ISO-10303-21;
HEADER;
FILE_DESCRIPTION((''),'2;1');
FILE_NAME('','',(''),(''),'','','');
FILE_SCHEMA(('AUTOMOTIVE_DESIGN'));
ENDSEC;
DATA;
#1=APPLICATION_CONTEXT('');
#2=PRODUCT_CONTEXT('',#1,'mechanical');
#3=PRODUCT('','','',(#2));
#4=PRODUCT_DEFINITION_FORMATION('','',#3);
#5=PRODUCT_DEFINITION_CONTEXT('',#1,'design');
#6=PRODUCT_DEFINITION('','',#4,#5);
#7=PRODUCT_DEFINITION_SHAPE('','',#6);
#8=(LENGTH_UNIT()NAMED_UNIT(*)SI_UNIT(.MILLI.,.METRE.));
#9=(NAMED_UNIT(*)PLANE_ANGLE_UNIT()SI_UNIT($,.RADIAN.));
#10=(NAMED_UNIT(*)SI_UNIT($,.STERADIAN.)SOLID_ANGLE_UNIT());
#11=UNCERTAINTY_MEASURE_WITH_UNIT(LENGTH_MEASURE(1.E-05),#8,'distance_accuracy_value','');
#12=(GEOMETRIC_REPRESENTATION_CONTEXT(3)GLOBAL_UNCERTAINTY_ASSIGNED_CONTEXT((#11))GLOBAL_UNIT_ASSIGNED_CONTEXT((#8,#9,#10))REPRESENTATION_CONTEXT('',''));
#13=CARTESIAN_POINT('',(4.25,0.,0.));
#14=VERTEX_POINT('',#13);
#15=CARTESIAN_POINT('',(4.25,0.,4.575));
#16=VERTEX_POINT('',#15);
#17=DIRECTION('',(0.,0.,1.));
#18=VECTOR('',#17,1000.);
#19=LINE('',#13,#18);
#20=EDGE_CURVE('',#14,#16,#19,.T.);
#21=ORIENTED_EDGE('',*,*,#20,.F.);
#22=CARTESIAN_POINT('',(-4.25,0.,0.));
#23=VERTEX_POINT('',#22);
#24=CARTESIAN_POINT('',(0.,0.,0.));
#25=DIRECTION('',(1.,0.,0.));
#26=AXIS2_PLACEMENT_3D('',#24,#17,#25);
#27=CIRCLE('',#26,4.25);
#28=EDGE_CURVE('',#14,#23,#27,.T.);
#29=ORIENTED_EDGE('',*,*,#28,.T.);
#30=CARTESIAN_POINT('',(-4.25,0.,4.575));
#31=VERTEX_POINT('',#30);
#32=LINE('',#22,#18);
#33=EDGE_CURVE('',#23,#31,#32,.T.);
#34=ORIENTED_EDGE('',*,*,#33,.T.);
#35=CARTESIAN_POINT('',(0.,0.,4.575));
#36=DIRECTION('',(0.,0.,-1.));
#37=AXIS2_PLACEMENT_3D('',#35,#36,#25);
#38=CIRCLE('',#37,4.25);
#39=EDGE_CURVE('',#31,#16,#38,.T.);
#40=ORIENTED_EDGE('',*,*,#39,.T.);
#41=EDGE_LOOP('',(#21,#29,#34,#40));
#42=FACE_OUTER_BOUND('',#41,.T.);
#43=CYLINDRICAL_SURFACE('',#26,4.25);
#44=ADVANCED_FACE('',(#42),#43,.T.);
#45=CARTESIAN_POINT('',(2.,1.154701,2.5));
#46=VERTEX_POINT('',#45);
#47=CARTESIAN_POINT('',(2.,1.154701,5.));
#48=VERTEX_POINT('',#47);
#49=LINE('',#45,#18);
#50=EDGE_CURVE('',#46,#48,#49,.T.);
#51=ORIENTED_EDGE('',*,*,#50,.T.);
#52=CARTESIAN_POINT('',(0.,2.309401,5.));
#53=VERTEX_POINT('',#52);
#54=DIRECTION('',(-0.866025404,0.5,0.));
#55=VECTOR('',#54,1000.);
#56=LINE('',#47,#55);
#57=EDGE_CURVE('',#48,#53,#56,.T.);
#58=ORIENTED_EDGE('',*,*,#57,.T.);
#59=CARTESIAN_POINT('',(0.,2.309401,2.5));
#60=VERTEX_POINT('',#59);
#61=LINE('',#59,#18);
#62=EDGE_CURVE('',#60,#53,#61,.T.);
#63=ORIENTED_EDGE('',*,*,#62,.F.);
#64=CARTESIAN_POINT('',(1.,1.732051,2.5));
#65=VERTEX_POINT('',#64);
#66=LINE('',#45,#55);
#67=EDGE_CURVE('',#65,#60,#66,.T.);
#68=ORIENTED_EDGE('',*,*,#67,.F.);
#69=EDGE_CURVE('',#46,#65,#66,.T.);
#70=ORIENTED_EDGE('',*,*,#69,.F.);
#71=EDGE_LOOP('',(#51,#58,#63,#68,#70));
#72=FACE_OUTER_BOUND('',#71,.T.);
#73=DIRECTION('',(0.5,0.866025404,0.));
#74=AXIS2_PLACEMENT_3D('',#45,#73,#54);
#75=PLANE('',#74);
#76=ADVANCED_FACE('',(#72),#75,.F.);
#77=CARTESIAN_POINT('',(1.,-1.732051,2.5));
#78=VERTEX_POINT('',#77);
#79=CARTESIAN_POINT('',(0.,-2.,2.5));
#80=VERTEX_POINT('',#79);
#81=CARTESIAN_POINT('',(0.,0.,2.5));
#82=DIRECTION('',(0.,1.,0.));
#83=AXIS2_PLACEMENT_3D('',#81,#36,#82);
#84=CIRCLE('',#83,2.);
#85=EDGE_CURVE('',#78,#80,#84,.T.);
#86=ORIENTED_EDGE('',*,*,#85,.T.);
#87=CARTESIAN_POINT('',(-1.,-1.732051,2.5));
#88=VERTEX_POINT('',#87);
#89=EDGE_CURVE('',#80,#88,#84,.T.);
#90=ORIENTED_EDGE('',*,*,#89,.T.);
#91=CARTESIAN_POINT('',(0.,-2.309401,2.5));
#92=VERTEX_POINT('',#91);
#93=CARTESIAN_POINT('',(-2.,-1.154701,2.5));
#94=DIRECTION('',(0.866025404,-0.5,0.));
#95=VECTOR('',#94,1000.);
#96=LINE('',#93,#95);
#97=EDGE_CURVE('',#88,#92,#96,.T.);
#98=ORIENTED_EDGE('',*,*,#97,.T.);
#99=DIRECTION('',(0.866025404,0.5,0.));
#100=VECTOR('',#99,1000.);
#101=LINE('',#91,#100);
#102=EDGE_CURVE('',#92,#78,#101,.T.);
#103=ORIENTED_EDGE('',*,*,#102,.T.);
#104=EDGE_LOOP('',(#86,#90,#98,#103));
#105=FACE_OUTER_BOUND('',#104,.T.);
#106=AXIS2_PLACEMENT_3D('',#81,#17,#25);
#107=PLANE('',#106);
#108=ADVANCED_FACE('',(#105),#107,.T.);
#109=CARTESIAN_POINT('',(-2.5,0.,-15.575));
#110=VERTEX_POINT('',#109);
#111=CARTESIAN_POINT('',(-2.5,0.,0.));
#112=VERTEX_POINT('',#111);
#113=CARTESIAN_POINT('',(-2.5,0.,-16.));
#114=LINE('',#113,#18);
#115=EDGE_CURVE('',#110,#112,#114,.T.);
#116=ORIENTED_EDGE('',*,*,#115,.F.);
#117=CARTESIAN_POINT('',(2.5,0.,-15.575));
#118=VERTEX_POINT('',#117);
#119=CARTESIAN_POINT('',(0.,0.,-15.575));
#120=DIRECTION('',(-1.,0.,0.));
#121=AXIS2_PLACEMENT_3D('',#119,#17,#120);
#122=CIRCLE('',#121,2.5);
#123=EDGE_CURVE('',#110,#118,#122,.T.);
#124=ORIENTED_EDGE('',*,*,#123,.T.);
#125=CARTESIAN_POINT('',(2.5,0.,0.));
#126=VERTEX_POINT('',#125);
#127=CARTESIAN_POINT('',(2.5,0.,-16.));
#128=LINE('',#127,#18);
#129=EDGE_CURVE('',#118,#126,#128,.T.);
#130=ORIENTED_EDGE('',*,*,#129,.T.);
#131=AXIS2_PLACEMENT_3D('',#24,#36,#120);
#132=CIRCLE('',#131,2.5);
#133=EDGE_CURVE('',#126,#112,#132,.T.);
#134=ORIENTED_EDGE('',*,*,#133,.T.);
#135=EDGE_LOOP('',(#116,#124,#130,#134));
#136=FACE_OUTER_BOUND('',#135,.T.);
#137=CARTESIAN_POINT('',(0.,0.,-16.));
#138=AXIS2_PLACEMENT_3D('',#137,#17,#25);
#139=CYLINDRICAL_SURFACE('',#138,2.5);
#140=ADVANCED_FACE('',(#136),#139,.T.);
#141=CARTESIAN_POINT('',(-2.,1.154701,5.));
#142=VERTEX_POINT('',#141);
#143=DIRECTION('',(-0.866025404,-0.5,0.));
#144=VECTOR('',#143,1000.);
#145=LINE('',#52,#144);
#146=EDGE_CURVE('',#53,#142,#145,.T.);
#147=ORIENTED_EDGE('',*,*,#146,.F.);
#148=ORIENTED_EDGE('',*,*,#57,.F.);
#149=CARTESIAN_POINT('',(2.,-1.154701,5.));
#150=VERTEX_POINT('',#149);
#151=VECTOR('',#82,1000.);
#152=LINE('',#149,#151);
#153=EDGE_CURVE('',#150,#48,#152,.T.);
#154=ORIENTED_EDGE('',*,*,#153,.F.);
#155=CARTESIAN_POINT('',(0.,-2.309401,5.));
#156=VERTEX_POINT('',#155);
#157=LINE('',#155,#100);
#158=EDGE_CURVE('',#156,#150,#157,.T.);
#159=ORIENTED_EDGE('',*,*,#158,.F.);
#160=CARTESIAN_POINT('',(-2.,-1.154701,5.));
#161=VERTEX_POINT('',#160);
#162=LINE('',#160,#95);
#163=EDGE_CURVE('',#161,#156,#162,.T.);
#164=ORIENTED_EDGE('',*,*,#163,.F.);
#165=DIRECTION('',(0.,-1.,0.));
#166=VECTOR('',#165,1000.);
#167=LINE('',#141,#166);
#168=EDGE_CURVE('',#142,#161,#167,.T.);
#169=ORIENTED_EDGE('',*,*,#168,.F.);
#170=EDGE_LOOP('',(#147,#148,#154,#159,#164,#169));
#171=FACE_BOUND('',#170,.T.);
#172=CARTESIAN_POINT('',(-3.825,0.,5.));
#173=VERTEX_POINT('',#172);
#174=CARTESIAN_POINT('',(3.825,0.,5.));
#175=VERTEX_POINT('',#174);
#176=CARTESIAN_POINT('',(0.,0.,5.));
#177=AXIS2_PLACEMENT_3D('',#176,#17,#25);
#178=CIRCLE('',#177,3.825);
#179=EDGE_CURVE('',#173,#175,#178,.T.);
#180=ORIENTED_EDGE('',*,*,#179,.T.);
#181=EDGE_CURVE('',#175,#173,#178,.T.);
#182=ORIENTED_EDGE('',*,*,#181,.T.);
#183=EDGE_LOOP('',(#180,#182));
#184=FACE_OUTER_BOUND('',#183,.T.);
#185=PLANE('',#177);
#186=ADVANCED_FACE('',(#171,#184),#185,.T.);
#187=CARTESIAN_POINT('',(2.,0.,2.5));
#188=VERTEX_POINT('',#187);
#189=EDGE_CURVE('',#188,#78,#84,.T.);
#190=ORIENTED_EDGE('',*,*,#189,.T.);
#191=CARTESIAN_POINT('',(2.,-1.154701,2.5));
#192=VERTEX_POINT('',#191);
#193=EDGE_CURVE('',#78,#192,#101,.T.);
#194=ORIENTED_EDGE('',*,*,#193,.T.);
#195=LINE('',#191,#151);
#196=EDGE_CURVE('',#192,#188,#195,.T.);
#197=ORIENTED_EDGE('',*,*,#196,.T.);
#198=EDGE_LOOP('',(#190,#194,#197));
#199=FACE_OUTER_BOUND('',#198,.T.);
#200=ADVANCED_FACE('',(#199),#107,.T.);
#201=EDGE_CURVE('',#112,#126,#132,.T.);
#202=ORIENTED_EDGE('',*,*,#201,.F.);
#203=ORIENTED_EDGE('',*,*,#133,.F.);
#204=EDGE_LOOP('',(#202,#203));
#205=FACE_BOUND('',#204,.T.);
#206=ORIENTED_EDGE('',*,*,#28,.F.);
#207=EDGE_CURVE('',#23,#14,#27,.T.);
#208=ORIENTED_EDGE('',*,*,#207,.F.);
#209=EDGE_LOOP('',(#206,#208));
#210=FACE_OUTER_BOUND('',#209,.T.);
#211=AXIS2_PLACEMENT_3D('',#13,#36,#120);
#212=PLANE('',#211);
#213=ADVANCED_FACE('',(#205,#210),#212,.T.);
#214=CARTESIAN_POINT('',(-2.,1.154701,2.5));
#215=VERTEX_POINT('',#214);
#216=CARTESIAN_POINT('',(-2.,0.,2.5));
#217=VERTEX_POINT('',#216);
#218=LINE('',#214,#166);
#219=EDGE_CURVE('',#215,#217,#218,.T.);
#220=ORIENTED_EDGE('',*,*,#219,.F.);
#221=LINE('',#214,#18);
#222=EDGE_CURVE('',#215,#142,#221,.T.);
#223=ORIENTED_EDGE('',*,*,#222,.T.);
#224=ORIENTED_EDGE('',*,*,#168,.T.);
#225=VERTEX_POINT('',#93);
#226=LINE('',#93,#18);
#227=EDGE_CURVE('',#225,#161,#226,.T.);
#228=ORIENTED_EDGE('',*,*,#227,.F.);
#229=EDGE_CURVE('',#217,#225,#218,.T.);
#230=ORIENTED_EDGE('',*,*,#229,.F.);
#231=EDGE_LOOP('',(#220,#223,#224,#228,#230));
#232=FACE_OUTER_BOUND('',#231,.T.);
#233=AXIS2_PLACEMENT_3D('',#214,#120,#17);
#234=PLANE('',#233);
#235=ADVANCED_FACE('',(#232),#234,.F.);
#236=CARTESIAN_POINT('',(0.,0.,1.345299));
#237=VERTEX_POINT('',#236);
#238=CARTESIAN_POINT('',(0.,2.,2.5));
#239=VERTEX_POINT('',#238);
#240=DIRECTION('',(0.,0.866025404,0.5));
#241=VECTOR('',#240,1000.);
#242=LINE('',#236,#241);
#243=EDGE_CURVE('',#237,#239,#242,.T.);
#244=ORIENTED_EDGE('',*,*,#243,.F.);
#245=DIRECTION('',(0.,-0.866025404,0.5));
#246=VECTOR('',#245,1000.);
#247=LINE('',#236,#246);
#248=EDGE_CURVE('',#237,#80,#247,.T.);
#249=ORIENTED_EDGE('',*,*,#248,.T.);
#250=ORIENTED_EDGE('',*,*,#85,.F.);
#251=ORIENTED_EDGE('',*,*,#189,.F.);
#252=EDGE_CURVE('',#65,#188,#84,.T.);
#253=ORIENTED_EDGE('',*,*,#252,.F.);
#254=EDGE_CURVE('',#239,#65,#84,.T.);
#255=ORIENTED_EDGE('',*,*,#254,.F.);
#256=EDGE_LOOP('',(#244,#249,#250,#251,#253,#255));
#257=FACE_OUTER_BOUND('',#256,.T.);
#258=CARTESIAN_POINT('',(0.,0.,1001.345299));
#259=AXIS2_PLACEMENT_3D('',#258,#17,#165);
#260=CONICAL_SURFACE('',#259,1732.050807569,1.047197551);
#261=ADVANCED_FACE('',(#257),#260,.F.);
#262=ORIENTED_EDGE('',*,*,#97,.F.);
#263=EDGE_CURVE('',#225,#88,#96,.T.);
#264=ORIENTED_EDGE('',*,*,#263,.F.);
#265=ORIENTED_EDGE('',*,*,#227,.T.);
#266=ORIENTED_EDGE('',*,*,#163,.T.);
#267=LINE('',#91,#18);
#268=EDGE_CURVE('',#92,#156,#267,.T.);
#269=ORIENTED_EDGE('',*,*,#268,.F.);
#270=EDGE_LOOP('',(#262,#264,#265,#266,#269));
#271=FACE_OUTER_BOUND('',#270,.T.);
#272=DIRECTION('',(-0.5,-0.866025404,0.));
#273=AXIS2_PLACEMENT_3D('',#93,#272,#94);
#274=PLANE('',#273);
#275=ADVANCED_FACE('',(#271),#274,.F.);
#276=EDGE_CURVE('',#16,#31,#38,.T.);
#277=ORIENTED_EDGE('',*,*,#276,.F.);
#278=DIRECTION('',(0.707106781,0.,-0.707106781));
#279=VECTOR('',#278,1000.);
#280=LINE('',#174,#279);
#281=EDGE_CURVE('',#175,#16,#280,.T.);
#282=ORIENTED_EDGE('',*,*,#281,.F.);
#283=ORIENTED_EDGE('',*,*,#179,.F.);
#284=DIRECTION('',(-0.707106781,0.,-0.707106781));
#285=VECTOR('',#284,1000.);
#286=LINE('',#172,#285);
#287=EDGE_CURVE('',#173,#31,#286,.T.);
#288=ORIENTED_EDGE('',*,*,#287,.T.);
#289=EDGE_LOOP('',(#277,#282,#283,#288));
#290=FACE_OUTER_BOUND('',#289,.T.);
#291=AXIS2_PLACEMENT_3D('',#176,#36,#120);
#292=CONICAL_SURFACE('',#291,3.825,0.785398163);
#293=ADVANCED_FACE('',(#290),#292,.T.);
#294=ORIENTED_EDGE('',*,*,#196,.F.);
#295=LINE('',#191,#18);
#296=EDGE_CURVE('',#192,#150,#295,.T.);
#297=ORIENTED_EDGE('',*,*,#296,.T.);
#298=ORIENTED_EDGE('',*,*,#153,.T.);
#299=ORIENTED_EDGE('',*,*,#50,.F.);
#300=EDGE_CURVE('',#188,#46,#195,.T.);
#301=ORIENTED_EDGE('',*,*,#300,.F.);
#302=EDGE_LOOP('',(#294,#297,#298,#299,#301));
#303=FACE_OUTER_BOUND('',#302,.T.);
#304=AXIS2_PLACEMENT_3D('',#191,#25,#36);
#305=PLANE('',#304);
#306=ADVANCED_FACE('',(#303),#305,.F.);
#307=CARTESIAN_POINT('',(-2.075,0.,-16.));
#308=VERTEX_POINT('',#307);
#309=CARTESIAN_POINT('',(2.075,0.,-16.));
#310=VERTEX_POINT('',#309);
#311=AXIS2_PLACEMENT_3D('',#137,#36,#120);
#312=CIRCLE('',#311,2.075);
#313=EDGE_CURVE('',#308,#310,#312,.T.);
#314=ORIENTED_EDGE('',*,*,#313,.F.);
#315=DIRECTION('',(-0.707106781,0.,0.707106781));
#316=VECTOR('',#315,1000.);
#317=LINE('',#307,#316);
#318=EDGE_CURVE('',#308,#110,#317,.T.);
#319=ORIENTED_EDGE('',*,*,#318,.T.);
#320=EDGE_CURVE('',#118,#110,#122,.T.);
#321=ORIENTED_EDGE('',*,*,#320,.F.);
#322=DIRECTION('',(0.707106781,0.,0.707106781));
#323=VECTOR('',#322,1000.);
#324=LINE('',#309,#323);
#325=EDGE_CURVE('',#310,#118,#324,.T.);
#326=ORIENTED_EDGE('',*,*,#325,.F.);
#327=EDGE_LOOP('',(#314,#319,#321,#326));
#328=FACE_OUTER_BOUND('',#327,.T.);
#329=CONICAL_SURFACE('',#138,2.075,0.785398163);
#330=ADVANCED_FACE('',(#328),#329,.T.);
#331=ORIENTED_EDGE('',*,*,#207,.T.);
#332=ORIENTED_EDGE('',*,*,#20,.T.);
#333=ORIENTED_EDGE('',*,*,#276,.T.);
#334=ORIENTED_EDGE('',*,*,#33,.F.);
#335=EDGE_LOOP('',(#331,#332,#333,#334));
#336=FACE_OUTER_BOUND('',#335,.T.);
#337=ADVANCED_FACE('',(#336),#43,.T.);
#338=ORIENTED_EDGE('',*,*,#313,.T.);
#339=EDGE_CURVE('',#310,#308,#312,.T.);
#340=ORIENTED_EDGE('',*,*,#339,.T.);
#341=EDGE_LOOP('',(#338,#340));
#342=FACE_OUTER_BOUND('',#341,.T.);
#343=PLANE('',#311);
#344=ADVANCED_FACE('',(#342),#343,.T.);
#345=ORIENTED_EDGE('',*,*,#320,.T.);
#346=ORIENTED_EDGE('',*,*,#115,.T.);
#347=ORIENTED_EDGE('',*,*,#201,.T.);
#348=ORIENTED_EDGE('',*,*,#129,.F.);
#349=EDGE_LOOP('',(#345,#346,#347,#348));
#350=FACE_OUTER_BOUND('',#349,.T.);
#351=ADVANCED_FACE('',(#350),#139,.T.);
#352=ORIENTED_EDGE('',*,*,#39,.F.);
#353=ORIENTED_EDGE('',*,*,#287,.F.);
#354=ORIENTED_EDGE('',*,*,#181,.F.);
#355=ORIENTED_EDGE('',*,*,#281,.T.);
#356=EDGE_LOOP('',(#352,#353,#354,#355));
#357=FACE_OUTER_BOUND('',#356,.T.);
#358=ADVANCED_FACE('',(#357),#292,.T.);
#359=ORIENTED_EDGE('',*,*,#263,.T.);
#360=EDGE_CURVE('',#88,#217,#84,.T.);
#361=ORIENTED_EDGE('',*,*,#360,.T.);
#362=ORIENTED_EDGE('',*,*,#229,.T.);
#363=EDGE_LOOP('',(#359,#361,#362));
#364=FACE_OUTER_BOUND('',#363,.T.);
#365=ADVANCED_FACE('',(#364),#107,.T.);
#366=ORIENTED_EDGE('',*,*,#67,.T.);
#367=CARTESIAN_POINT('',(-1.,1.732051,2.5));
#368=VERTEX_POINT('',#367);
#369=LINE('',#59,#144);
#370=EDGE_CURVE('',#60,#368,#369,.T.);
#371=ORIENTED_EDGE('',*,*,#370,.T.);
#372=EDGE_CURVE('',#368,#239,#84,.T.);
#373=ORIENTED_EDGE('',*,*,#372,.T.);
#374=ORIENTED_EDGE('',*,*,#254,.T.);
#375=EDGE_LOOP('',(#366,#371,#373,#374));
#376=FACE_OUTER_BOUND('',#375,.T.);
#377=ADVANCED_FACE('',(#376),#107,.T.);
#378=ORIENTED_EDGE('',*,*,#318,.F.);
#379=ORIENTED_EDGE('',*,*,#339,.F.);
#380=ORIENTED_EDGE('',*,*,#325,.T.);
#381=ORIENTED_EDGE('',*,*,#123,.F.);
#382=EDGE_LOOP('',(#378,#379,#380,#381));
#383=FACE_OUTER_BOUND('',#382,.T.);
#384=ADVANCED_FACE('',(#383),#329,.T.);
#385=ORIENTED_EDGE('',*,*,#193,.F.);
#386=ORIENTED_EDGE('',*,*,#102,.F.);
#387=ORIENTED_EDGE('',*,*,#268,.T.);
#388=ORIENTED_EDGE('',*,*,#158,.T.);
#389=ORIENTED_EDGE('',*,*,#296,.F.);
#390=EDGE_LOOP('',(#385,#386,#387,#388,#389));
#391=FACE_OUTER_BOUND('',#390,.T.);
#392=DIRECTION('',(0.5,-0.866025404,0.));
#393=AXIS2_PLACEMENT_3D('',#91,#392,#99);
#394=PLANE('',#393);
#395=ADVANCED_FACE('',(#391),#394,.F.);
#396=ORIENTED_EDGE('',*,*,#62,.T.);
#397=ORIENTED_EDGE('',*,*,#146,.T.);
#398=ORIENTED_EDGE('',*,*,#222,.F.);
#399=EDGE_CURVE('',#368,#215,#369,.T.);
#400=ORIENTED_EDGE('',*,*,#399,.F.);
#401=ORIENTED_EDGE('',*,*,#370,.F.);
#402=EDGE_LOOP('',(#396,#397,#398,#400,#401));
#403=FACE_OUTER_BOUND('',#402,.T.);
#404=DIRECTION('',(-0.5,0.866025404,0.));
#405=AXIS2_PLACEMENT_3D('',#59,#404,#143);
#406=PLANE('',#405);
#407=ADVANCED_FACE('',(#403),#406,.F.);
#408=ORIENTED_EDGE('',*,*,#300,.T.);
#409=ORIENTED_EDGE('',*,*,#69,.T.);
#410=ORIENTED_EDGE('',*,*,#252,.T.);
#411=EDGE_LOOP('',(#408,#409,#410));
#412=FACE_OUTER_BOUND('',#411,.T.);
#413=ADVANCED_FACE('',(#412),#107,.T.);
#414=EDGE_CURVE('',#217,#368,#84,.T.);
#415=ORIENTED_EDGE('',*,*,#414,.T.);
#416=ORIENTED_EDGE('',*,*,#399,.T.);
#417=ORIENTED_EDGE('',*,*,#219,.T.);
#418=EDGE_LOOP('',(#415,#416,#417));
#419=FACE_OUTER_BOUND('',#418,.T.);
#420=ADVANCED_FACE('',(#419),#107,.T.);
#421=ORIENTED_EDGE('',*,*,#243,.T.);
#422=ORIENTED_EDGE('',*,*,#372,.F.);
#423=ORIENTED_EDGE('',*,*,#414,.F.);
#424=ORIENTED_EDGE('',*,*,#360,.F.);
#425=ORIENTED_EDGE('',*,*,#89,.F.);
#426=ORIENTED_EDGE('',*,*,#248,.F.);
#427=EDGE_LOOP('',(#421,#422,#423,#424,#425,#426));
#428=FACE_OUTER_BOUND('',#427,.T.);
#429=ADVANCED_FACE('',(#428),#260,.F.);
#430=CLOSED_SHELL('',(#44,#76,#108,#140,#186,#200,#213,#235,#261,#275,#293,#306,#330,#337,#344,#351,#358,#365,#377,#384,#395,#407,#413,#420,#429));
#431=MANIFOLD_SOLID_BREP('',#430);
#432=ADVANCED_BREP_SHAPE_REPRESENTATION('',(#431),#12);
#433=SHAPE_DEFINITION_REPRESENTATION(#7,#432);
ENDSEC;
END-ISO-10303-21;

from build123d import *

# Parameters (mm, degrees)
SKETCH_1_W          = 4.25
SKETCH_1_H          = 5
SKETCH_2_R          = 2.5
EXTRUDE_1_DEPTH     = 16
CUT_EXTRUDE_1_DEPTH = 2.5
CHAMFER_1_SIZE      = 0.425


with BuildPart() as part:
    # 草图1 → 旋转1 (revolve)
    with BuildSketch(Plane(origin=(0, 0, 0), x_dir=(1, 0, 0), z_dir=(0, 1, 0))):
        with Locations((2.125, -2.5)):
            Rectangle(SKETCH_1_W, SKETCH_1_H)
    revolve(axis=Axis((0, 0, 0), (0, 0, 1)))

    # 草图2 → 凸台-拉伸1 (add)
    with BuildSketch(Plane(origin=(0, 0, 0), x_dir=(-1, 0, 0), z_dir=(0, 0, -1))):
        Circle(SKETCH_2_R)
    extrude(amount=EXTRUDE_1_DEPTH)

    # 草图3 → 切除-拉伸1 (cut)
    with BuildSketch(Plane.XY.offset(5)):
        Polygon((2, 1.154700538), (0, 2.309401077), (-2, 1.154700538), (-2, -1.154700538), (0, -2.309401077), (2, -1.154700538), align=None)
    extrude(amount=-CUT_EXTRUDE_1_DEPTH, mode=Mode.SUBTRACT)

    # 草图4 → 切除-旋转1 (revolve, cut)
    with BuildSketch(Plane.XZ, mode=Mode.PRIVATE) as cut_revolve_1_sk:
        Polygon((2, 2.5), (0, 2.5), (0, 1.345299462), align=None)
    revolve(cut_revolve_1_sk.sketch.rotate(Axis((0, 0, 2.5), (0, 0, -1)), 90), axis=Axis((0, 0, 2.5), (0, 0, -1)), mode=Mode.SUBTRACT)

    # 倒角1
    chamfer_1_edges = [part.edges().sort_by_distance(p)[0] for p in [
        (-4.25, 0, 5),
        (2.5, 0, -16),
    ]]
    chamfer(chamfer_1_edges, length=CHAMFER_1_SIZE)


solid = part.part
